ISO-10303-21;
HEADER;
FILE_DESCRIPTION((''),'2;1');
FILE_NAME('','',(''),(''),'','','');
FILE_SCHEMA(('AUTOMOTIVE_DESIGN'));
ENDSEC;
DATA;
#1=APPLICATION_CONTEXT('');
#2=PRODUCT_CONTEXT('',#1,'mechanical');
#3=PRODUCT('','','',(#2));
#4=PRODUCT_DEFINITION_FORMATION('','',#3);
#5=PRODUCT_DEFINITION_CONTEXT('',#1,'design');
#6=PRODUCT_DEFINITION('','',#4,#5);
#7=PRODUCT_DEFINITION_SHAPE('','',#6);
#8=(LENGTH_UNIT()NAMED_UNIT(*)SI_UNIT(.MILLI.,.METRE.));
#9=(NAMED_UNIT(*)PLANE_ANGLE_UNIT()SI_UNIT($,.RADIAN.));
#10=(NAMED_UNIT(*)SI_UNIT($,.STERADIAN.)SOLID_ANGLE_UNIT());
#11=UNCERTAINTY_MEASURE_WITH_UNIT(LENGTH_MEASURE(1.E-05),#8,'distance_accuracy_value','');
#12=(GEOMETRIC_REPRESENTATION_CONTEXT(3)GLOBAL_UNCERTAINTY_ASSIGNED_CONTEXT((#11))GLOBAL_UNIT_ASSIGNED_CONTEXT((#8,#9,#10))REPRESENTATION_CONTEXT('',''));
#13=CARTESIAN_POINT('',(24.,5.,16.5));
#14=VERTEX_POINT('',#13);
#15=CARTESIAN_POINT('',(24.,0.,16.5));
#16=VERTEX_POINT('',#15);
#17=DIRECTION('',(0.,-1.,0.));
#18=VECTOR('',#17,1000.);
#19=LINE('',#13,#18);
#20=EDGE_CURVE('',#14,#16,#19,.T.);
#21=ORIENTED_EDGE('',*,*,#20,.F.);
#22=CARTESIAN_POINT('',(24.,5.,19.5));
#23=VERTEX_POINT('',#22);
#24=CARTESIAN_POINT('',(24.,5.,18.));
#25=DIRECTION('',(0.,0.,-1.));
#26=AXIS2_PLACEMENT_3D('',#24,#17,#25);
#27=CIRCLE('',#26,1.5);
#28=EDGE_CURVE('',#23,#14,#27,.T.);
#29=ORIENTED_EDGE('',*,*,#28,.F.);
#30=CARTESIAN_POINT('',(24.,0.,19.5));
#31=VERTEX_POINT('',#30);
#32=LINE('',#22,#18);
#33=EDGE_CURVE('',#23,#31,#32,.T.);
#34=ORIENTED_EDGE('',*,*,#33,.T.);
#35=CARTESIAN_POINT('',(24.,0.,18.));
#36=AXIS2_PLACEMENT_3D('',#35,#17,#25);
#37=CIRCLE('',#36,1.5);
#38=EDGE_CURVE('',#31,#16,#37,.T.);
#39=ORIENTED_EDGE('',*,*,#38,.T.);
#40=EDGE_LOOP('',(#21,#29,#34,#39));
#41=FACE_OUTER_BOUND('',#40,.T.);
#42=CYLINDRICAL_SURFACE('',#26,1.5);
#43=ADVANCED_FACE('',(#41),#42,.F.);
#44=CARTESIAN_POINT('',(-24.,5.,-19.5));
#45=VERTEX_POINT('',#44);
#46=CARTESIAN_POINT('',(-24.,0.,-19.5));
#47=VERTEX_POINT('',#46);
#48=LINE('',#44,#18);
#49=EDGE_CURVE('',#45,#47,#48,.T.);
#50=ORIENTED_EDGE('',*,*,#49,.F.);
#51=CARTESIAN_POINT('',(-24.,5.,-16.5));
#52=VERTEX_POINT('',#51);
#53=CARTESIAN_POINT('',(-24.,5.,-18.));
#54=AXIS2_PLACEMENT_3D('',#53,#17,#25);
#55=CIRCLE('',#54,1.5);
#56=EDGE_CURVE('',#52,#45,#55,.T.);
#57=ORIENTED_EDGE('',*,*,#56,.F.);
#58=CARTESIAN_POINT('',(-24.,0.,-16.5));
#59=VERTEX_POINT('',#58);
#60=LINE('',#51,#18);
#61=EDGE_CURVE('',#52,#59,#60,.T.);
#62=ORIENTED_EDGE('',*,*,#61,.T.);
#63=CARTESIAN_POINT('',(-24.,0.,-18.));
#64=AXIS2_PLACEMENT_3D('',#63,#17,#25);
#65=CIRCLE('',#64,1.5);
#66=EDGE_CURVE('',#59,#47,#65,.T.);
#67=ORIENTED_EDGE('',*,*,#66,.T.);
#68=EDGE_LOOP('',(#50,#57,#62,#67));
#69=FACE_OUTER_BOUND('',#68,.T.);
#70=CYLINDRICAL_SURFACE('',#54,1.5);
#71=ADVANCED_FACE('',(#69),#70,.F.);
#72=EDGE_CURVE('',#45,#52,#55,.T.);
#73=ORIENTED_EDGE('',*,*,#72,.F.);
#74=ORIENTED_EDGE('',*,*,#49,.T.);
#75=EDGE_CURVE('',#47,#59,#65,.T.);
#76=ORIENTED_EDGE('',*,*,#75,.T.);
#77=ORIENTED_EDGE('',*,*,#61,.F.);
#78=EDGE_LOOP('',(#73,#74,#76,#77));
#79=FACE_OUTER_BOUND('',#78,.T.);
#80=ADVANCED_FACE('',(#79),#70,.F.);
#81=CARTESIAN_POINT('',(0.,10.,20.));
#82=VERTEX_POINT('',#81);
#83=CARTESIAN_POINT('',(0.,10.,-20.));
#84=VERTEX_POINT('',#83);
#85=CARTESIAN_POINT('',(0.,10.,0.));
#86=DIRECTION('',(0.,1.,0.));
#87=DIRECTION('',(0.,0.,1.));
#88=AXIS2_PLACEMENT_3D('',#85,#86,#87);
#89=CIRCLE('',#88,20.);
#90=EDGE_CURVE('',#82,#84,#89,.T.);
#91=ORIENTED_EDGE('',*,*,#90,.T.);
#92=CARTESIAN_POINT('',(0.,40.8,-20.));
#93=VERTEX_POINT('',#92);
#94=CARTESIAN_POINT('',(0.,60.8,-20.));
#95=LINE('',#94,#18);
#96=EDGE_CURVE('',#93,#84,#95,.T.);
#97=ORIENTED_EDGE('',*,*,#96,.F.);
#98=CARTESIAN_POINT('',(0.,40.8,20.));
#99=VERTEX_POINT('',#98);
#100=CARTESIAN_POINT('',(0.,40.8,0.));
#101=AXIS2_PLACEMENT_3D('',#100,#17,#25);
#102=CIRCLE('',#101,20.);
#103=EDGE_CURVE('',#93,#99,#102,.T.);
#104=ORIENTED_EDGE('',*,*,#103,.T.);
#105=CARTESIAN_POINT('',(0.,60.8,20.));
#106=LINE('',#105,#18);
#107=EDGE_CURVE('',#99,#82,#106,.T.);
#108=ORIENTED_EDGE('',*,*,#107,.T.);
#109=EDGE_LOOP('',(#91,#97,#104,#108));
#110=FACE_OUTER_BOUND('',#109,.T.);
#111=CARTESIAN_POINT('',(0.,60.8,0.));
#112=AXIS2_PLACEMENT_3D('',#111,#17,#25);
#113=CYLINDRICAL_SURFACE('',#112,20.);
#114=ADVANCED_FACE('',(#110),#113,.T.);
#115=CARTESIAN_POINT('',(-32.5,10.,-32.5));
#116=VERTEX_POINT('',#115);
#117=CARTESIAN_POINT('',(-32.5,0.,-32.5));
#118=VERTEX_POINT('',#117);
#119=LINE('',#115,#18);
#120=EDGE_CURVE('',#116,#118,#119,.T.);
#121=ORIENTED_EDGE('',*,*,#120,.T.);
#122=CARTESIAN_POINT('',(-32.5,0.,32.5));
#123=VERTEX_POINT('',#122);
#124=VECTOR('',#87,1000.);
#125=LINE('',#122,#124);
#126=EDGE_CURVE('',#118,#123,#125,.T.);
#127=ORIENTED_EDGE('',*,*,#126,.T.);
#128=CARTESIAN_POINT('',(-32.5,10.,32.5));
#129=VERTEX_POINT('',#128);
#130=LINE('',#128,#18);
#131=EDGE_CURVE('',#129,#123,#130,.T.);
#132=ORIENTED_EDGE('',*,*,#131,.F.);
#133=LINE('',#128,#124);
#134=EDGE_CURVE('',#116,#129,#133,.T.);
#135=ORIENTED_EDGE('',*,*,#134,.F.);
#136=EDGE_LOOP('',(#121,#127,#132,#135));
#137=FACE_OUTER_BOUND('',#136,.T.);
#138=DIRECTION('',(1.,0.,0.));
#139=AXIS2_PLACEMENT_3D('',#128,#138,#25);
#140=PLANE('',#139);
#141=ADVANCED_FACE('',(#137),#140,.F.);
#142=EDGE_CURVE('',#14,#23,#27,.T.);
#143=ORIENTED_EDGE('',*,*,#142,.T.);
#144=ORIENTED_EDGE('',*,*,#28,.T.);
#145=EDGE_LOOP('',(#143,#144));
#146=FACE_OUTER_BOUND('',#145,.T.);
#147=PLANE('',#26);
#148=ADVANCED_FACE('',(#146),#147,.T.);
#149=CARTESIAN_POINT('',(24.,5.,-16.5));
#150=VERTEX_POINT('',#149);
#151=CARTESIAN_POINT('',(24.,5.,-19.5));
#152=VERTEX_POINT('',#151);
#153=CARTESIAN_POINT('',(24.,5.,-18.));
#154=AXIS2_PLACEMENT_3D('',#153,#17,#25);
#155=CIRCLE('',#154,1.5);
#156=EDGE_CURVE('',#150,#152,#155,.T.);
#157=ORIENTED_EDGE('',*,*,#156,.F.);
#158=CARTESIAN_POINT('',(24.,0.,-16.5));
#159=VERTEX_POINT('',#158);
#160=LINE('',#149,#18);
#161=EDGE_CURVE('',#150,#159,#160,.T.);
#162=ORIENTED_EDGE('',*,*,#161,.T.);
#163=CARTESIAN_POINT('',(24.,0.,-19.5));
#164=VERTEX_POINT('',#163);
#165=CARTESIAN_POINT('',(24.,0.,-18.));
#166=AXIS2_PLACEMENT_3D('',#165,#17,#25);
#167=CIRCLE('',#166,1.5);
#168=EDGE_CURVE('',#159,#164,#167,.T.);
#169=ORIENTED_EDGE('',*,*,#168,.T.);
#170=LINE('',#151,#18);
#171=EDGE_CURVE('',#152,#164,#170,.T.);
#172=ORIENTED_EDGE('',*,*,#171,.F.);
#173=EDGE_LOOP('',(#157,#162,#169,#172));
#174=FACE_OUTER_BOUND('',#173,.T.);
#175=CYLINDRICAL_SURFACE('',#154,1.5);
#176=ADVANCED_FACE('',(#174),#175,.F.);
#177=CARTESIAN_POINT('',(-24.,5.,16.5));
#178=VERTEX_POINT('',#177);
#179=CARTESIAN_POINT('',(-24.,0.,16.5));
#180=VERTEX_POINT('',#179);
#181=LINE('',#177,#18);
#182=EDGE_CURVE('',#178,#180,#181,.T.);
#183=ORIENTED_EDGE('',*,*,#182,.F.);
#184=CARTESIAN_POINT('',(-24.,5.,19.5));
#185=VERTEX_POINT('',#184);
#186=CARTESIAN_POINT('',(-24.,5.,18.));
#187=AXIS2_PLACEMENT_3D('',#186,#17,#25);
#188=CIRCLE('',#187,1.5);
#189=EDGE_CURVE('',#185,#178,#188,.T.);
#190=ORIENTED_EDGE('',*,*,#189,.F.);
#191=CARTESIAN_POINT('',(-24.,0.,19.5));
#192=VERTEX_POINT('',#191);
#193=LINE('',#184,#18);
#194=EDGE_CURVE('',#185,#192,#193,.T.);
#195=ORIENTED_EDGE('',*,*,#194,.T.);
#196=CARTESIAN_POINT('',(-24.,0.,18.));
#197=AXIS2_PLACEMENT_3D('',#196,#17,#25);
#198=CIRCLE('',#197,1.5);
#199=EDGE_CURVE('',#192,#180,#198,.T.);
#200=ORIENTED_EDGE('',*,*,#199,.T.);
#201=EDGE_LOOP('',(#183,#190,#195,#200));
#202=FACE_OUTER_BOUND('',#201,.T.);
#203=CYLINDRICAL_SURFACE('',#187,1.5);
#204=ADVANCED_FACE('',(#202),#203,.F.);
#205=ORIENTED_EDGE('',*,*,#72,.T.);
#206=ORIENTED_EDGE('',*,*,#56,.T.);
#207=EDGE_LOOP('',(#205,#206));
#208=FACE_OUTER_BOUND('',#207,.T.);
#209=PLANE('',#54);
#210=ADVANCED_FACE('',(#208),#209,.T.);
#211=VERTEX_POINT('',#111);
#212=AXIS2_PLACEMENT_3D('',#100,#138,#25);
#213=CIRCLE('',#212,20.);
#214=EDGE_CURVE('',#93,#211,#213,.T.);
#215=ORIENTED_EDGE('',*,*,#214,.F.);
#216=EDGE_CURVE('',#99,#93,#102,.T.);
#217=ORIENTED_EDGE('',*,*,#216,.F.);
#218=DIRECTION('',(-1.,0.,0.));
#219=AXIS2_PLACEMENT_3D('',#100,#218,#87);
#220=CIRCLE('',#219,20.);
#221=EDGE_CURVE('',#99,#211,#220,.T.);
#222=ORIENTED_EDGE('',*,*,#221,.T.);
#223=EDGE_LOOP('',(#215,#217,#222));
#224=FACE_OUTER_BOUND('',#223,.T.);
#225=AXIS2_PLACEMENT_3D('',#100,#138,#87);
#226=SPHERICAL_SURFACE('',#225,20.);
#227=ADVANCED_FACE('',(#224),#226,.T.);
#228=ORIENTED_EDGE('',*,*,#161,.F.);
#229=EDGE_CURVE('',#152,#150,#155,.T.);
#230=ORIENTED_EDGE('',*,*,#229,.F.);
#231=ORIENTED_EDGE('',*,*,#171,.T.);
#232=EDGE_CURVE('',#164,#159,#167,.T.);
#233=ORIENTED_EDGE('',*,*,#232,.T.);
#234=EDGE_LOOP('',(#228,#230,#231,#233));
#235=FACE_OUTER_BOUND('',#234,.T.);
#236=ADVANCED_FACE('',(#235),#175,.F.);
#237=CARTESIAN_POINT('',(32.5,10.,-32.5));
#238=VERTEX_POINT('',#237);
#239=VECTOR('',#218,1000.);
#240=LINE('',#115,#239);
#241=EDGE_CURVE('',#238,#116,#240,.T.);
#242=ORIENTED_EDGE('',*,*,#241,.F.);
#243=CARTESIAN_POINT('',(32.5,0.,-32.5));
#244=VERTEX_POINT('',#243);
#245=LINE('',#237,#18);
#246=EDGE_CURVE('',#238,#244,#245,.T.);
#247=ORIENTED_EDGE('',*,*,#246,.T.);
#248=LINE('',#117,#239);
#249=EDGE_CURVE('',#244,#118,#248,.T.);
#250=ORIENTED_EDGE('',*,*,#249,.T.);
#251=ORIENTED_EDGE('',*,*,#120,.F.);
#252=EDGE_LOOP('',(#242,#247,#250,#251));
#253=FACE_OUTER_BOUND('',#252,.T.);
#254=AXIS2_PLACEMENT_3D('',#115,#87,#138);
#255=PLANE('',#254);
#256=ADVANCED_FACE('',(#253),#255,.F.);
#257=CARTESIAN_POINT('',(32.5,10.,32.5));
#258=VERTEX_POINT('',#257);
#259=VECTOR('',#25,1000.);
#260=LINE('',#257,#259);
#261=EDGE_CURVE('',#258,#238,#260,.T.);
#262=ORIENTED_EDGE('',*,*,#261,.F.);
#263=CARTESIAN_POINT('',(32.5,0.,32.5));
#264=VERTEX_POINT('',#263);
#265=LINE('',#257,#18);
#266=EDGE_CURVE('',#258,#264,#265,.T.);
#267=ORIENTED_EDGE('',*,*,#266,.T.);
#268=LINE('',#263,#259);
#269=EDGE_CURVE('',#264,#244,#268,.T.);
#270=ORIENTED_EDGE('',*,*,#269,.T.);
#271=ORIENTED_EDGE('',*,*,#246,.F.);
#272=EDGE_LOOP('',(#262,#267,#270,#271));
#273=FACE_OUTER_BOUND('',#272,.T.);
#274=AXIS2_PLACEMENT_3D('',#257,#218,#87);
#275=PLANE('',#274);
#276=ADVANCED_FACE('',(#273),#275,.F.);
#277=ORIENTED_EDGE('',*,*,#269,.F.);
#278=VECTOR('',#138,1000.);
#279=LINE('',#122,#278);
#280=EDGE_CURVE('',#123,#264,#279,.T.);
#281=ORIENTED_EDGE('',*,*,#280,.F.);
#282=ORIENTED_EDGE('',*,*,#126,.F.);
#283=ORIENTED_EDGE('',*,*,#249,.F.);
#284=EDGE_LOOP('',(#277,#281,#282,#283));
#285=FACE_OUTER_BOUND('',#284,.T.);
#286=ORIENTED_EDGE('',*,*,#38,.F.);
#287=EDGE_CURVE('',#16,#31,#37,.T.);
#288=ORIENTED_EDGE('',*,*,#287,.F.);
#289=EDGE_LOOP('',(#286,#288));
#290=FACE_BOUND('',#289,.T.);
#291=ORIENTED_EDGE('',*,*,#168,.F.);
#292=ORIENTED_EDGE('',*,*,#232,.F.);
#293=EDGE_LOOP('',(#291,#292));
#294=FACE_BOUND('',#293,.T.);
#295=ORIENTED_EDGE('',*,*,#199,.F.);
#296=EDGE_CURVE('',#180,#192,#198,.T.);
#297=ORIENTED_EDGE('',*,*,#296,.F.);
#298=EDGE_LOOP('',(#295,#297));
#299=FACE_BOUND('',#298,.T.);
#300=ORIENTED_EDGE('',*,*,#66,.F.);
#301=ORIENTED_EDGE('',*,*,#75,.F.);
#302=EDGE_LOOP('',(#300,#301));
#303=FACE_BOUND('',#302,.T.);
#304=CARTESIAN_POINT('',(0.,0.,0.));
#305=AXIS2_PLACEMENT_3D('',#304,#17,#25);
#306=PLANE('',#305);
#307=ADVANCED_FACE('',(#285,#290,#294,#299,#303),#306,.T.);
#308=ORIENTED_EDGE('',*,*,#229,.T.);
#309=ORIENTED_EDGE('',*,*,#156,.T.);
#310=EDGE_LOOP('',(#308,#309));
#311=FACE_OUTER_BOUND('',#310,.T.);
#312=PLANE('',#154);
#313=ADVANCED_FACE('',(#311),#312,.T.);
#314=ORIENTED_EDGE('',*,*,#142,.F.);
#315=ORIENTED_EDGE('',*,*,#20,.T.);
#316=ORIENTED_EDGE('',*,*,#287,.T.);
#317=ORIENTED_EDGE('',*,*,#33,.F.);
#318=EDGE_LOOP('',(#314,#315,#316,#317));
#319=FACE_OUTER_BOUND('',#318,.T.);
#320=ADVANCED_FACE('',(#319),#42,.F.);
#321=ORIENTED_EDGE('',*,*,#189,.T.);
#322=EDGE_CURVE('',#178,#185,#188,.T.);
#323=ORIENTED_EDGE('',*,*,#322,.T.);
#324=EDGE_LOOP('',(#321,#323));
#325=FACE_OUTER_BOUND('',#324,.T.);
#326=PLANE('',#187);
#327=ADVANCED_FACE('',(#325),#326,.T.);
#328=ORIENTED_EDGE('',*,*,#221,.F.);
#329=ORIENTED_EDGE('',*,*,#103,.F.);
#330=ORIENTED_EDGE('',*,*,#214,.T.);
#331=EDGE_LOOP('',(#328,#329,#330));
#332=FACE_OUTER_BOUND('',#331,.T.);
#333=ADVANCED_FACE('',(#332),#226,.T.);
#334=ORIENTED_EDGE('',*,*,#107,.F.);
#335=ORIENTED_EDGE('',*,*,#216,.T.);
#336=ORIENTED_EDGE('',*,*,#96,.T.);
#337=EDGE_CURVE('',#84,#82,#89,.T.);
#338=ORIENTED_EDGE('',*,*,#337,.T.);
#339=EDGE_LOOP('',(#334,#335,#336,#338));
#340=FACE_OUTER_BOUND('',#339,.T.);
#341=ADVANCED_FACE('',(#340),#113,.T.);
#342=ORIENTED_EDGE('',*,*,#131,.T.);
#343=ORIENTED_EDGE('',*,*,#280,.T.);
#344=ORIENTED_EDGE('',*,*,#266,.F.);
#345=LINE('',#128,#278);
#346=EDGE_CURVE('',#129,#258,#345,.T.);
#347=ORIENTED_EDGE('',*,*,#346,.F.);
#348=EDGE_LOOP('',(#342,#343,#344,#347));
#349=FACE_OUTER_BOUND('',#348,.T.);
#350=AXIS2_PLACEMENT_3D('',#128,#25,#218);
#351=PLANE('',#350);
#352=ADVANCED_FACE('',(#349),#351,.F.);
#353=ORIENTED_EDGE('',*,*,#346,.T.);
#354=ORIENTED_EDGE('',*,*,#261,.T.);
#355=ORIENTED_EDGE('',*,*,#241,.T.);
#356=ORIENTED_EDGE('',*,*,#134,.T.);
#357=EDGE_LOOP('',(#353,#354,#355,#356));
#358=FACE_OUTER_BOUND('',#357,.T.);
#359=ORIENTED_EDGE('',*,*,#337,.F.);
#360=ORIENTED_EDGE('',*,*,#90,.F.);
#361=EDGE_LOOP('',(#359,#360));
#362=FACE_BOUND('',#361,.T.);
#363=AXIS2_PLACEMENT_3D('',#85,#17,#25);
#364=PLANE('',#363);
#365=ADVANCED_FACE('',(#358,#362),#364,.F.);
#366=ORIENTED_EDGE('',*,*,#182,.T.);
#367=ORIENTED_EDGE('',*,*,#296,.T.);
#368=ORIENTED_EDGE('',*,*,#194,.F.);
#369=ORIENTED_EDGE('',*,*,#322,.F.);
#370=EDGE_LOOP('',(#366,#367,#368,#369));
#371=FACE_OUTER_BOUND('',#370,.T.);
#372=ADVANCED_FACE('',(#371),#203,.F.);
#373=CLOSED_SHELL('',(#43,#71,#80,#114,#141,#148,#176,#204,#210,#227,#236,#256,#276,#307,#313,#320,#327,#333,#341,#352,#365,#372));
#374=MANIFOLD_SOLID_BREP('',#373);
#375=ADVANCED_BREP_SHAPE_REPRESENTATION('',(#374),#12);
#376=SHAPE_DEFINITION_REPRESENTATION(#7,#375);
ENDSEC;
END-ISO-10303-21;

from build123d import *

# Parameters (mm, degrees)
SKETCH1_W           = 65
SKETCH1_H           = 65
BOSS_EXTRUDE1_DEPTH = 10
SKETCH2_R           = 20
BOSS_EXTRUDE2_DEPTH = 50.8
FILLET1_R           = 20
SKETCH3_R           = 1.5
CUT_EXTRUDE1_DEPTH  = 5


with BuildPart() as part:
    # Sketch1 → Boss-Extrude1 (new body)
    with BuildSketch(Plane(origin=(0, 0, 0), x_dir=(1, 0, 0), z_dir=(0, 1, 0))):
        Rectangle(SKETCH1_W, SKETCH1_H)
    extrude(amount=BOSS_EXTRUDE1_DEPTH)

    # Sketch2 → Boss-Extrude2 (add)
    with BuildSketch(Plane(origin=(0, 10, 0), x_dir=(1, 0, 0), z_dir=(0, 1, 0))):
        with Locations(Location((0, 0, 0), (0, 0, 270))):
            Circle(SKETCH2_R)
    extrude(amount=BOSS_EXTRUDE2_DEPTH)

    # Fillet1
    fillet1_edges = [part.edges().sort_by_distance(p)[0] for p in [
        (0, 60.8, -20),
    ]]
    fillet(fillet1_edges, radius=FILLET1_R)

    # Sketch3 → Cut-Extrude1 (cut)
    with BuildSketch(Plane.XZ):
        with Locations(Location((24, 18, 0), (0, 0, 270))):
            Circle(SKETCH3_R)
        with Locations(Location((-24, 18, 0), (0, 0, 270))):
            Circle(SKETCH3_R)
        with Locations(Location((-24, -18, 0), (0, 0, 270))):
            Circle(SKETCH3_R)
        with Locations(Location((24, -18, 0), (0, 0, 270))):
            Circle(SKETCH3_R)
    extrude(amount=-CUT_EXTRUDE1_DEPTH, mode=Mode.SUBTRACT)


solid = part.part
